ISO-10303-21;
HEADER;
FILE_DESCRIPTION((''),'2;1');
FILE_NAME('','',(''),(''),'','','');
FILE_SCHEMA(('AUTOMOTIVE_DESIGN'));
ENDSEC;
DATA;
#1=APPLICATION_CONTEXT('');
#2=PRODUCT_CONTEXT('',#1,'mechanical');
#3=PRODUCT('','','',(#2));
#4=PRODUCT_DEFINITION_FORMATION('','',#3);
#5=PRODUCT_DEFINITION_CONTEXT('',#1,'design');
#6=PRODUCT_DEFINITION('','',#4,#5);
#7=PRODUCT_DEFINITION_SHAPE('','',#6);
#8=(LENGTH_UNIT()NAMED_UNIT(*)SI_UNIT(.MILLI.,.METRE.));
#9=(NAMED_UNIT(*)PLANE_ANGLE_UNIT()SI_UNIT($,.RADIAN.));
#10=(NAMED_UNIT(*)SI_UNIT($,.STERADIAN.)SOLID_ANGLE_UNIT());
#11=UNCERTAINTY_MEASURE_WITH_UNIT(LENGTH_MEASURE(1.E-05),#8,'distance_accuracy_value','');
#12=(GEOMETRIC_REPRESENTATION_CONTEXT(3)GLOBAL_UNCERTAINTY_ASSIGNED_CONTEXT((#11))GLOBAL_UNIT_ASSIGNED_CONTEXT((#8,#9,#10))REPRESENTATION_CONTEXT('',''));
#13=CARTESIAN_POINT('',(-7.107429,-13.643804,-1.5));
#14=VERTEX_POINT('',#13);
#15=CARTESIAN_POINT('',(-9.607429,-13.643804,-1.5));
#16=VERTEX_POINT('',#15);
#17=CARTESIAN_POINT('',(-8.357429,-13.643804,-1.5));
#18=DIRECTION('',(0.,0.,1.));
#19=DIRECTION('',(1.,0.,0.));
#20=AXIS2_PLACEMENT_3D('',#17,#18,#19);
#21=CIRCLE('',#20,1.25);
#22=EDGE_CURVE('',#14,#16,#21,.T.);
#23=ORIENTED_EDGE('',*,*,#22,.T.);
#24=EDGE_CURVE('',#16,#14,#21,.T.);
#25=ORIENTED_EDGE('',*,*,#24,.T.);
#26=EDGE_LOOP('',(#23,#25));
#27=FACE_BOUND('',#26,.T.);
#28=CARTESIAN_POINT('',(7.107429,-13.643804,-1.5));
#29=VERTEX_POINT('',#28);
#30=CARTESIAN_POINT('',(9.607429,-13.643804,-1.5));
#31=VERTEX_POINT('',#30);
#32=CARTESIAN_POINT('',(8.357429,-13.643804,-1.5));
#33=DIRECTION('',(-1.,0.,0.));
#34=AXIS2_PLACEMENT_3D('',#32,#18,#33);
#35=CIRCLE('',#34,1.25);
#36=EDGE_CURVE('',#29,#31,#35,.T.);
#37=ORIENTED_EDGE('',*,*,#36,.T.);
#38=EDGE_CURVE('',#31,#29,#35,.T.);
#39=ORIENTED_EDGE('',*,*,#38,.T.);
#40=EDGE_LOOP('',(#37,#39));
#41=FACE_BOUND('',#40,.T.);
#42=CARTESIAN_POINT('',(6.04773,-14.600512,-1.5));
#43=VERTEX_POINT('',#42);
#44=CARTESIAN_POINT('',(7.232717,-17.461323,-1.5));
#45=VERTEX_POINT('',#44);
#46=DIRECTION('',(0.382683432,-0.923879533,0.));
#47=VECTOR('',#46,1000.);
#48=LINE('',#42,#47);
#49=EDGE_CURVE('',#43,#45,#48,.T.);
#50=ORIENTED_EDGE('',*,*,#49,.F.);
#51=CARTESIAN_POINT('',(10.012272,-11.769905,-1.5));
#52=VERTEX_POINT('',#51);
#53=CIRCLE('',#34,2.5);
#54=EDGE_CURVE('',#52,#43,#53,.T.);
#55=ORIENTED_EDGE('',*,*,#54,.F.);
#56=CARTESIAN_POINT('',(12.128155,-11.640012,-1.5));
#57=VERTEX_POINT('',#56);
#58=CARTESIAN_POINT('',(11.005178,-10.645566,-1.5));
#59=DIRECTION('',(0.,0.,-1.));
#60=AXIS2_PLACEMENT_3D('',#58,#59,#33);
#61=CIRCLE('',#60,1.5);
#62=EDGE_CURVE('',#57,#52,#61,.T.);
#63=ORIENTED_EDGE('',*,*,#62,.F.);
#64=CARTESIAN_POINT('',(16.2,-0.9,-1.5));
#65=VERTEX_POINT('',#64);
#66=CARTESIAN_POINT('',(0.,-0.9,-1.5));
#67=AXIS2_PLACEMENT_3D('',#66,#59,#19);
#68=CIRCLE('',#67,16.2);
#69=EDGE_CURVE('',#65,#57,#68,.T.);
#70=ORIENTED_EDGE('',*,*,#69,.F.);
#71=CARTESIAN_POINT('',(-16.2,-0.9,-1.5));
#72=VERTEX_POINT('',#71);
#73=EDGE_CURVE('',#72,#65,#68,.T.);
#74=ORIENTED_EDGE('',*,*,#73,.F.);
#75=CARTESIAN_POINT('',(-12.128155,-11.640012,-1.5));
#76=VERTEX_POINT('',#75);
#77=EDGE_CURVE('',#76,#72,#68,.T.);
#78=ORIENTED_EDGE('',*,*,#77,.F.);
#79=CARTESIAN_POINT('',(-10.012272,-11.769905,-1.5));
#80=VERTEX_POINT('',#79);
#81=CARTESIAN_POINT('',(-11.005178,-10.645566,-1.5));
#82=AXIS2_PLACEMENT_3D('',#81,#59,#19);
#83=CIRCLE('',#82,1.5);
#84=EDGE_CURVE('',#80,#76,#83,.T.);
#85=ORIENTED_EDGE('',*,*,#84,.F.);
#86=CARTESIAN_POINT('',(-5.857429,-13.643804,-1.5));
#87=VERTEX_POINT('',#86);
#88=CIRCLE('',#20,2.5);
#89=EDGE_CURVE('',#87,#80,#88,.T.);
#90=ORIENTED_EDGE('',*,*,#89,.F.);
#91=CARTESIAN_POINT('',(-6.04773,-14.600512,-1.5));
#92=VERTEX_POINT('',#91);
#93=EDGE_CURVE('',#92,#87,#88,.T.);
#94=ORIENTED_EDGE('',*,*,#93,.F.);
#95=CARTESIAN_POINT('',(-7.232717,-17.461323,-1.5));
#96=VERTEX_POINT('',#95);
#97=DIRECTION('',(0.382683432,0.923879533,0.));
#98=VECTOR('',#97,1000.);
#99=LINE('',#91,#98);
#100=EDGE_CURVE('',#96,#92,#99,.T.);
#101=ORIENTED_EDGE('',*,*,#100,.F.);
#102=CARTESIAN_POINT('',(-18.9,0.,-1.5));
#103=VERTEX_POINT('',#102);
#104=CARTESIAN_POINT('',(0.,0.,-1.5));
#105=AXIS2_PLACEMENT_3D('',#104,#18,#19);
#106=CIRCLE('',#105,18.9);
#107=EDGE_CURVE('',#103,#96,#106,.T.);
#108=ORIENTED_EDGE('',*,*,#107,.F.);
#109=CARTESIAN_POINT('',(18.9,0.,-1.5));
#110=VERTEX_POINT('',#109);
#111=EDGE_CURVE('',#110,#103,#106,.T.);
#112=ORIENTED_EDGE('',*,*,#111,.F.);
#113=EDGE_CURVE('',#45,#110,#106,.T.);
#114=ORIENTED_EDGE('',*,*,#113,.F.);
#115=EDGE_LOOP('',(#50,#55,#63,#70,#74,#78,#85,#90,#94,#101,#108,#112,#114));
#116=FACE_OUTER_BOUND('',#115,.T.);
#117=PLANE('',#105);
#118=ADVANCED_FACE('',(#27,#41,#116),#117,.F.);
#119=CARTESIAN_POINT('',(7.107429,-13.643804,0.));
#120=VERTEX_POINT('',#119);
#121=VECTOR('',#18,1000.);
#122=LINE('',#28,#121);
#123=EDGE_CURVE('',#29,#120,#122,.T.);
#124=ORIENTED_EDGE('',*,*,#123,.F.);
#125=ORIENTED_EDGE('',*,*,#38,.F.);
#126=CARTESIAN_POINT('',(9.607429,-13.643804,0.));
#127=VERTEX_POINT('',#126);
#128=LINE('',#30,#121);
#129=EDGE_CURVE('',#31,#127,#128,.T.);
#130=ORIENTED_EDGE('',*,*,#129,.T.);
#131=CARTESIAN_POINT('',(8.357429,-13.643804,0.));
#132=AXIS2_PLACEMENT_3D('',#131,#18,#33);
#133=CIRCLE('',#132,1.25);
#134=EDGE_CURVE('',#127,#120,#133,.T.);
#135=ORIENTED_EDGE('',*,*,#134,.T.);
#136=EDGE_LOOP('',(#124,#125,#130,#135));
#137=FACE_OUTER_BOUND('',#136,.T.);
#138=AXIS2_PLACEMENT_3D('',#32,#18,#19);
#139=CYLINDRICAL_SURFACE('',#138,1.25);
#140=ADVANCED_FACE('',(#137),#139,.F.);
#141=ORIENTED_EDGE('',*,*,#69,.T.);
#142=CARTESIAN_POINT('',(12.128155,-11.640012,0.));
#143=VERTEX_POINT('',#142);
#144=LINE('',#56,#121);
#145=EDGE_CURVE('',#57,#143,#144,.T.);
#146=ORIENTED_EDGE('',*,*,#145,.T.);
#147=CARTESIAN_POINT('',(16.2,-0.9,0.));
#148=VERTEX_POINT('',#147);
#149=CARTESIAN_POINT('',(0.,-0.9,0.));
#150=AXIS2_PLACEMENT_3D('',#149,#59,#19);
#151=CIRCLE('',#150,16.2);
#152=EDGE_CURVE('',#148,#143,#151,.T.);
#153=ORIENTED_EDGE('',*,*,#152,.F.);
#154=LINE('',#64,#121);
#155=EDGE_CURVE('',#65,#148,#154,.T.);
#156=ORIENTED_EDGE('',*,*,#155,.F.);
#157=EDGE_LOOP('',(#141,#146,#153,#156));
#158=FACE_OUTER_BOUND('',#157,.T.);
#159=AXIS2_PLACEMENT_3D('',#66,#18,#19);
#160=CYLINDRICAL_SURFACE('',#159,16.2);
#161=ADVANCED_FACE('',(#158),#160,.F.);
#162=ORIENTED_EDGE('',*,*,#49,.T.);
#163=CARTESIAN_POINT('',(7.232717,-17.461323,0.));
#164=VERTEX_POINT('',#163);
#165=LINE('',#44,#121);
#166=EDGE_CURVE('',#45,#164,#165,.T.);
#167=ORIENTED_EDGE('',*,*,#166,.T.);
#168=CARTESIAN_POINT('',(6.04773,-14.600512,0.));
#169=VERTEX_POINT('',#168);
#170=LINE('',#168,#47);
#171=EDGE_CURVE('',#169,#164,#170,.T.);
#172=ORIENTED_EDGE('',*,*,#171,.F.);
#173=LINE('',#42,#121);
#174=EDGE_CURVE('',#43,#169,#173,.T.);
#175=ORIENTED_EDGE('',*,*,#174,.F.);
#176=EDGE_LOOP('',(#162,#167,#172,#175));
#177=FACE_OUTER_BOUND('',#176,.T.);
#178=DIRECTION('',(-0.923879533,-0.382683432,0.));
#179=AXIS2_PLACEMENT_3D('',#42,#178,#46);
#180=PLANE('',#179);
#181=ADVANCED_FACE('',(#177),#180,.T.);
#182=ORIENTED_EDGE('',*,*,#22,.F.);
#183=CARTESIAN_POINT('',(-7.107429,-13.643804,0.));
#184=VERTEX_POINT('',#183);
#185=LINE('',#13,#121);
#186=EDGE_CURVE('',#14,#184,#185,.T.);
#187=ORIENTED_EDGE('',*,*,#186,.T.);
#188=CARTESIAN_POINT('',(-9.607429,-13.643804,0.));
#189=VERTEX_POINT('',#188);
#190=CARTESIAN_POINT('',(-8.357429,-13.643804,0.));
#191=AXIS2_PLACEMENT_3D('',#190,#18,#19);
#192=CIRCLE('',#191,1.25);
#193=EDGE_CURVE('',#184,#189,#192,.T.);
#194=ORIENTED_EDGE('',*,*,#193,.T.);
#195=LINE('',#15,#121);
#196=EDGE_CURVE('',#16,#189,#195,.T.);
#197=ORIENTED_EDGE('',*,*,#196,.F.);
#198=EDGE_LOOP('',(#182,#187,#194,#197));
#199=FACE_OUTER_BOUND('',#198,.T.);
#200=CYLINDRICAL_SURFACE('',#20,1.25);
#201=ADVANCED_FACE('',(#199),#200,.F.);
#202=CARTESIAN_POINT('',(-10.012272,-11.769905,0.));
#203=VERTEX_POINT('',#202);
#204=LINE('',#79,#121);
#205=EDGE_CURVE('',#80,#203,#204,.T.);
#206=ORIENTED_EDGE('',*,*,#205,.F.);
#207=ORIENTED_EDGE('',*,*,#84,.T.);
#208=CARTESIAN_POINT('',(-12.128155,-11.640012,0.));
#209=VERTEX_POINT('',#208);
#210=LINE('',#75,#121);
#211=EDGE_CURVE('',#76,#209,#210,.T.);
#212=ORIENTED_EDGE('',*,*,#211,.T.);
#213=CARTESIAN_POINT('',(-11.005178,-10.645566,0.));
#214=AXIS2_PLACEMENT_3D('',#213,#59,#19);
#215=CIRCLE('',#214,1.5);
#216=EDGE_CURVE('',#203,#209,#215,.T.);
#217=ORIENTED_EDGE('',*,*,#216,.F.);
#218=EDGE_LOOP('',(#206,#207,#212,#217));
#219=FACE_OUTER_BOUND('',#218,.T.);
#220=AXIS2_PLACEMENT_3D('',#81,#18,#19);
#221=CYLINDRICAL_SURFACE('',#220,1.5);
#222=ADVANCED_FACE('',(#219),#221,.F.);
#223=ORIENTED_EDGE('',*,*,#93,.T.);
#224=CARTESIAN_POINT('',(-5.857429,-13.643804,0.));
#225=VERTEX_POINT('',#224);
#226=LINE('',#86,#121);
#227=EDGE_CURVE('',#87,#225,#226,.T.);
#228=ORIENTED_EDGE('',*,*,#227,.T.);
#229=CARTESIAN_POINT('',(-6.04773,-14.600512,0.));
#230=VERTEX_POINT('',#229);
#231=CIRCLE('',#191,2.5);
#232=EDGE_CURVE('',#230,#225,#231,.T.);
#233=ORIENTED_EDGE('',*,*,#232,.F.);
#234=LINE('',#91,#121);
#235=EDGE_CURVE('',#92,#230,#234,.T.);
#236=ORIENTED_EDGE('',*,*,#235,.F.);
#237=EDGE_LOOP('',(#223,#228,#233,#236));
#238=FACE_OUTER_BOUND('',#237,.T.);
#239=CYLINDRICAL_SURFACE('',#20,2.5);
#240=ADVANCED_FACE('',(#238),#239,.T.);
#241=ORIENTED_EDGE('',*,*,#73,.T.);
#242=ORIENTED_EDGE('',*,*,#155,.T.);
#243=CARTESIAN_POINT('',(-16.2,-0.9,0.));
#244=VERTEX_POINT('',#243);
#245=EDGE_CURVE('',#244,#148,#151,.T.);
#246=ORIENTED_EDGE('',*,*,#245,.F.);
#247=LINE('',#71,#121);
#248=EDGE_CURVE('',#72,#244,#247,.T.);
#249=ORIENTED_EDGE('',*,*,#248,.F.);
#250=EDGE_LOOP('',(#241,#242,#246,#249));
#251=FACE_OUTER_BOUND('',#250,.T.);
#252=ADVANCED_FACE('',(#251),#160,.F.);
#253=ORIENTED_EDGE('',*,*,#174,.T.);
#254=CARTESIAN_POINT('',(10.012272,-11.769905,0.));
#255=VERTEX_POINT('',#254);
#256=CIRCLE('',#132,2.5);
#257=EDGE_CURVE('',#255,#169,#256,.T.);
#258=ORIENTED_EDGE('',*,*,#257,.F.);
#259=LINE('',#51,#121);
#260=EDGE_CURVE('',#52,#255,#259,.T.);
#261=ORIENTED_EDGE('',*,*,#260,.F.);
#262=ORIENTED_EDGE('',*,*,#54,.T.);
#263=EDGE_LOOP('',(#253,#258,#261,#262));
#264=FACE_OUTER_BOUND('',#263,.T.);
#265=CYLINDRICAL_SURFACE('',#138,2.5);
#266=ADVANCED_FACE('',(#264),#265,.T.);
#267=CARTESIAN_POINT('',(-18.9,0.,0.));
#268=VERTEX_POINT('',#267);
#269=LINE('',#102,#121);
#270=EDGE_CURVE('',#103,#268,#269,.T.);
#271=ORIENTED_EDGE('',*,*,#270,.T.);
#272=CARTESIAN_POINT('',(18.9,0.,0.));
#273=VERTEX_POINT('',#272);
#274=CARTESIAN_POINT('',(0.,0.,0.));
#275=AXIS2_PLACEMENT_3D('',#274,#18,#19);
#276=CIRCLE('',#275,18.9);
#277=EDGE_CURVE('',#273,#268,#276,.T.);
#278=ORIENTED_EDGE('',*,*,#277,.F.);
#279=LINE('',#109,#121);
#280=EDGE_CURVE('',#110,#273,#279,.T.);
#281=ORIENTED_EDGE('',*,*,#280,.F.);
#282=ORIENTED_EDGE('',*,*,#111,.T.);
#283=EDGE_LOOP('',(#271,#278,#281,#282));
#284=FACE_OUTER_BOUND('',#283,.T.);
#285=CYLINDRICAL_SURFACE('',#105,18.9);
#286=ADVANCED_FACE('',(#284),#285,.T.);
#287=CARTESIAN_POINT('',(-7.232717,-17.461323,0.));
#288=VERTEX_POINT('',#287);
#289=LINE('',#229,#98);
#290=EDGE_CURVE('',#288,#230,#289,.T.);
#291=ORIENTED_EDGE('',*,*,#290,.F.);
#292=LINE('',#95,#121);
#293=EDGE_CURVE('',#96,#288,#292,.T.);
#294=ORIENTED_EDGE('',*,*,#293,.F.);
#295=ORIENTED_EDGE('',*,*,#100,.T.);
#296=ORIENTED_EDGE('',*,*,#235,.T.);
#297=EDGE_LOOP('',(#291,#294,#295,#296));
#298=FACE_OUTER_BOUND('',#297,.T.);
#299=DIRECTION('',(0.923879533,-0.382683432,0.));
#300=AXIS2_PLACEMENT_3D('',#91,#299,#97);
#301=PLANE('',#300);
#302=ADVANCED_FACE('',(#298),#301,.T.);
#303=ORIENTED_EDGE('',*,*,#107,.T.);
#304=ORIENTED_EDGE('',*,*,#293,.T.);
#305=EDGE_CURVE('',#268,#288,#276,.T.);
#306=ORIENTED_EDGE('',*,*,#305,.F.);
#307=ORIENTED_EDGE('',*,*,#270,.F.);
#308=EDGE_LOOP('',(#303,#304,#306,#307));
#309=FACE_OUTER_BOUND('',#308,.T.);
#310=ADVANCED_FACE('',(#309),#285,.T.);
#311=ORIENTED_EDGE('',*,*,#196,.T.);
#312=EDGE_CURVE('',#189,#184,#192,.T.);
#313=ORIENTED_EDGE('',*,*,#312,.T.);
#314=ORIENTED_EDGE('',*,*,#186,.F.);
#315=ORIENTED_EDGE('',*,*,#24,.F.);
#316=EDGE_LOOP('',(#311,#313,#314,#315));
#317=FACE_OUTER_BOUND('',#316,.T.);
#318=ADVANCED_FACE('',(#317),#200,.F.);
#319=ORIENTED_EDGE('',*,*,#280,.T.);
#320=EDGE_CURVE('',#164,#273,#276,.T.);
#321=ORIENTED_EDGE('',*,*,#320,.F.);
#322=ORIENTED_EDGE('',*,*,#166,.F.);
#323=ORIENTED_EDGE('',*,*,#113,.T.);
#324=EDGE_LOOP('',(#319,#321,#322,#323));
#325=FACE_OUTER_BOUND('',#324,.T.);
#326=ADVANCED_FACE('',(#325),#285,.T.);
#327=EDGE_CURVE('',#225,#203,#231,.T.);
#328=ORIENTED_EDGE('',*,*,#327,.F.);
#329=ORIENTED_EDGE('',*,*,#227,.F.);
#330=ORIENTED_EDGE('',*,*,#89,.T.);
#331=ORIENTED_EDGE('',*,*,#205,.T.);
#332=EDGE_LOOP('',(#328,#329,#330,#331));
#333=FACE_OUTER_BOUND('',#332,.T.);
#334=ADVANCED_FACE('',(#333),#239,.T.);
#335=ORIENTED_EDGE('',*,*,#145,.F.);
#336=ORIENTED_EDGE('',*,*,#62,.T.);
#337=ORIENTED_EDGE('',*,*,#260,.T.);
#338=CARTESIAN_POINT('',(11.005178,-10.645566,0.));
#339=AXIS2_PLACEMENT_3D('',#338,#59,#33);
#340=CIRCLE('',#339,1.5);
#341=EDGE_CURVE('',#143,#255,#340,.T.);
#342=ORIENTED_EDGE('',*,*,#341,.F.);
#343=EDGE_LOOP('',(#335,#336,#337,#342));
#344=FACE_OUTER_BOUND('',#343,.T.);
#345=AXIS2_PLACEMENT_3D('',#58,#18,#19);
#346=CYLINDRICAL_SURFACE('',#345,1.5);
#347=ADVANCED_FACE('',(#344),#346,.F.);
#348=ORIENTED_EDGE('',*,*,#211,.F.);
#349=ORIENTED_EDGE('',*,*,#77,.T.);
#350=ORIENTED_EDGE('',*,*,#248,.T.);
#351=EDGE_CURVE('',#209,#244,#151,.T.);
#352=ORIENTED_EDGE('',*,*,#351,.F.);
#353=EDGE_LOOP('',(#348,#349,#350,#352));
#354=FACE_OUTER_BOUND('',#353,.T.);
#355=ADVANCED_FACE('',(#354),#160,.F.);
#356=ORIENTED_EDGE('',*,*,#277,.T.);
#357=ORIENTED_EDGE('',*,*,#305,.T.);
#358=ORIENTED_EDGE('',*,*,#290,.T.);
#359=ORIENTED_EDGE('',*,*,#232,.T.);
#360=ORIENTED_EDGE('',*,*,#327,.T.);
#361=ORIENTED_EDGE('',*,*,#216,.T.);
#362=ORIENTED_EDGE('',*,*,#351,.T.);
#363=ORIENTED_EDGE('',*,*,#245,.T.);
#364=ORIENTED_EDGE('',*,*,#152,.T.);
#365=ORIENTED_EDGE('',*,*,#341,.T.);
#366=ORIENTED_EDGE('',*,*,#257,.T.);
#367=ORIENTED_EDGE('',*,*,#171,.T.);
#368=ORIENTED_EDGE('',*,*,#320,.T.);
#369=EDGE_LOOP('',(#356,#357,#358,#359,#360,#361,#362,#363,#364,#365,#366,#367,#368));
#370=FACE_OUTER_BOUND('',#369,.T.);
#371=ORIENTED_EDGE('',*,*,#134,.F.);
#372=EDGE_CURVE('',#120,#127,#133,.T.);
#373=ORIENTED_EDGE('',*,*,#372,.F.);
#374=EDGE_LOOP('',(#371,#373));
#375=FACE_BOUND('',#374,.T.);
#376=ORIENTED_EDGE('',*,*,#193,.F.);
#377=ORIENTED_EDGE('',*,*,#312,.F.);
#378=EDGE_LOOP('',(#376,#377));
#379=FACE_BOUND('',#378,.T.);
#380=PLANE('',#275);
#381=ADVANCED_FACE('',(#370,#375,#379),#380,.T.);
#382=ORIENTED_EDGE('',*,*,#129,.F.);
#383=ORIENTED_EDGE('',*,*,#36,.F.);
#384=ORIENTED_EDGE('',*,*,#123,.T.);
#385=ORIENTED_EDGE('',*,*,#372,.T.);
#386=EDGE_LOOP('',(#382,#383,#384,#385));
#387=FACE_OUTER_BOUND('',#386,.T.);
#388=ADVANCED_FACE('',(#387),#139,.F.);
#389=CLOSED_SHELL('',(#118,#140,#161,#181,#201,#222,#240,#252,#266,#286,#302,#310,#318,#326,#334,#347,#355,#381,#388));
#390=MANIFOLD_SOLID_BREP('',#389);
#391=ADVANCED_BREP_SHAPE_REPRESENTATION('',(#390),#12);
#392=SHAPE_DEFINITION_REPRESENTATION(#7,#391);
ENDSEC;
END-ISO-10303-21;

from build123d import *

# Parameters (mm, degrees)
SKETCH1_R  = 1.25
BODY_DEPTH = 1.5


with BuildPart() as part:
    # Sketch1 → Body (new body)
    with BuildSketch(Plane.XY):
        with BuildLine():
            Line((6.047730211, -14.600512296), (7.232716872, -17.461323164))
            ThreePointArc((7.232716872, -17.461323164), (0, 18.9), (-7.232716872, -17.461323164))
            Line((-7.232716872, -17.461323164), (-6.047730211, -14.600512296))
            ThreePointArc((-6.047730211, -14.600512296), (-6.904744304, -11.609176709), (-10.012271945, -11.769905381))
            ThreePointArc((-10.012271945, -11.769905381), (-11.097089224, -12.142747822), (-12.128155002, -11.64001193))
            ThreePointArc((-12.128155002, -11.64001193), (0, 15.3), (12.128155002, -11.64001193))
            ThreePointArc((12.128155002, -11.64001193), (11.097089224, -12.142747822), (10.012271945, -11.769905381))
            ThreePointArc((10.012271945, -11.769905381), (6.904744304, -11.609176709), (6.047730211, -14.600512296))
        make_face()
        with Locations(Location((8.357429042, -13.643803715, 0), (0, 0, 180))):
            Circle(SKETCH1_R, mode=Mode.SUBTRACT)
        with Locations((-8.357429042, -13.643803715)):
            Circle(SKETCH1_R, mode=Mode.SUBTRACT)
    extrude(amount=-BODY_DEPTH)


solid = part.part
